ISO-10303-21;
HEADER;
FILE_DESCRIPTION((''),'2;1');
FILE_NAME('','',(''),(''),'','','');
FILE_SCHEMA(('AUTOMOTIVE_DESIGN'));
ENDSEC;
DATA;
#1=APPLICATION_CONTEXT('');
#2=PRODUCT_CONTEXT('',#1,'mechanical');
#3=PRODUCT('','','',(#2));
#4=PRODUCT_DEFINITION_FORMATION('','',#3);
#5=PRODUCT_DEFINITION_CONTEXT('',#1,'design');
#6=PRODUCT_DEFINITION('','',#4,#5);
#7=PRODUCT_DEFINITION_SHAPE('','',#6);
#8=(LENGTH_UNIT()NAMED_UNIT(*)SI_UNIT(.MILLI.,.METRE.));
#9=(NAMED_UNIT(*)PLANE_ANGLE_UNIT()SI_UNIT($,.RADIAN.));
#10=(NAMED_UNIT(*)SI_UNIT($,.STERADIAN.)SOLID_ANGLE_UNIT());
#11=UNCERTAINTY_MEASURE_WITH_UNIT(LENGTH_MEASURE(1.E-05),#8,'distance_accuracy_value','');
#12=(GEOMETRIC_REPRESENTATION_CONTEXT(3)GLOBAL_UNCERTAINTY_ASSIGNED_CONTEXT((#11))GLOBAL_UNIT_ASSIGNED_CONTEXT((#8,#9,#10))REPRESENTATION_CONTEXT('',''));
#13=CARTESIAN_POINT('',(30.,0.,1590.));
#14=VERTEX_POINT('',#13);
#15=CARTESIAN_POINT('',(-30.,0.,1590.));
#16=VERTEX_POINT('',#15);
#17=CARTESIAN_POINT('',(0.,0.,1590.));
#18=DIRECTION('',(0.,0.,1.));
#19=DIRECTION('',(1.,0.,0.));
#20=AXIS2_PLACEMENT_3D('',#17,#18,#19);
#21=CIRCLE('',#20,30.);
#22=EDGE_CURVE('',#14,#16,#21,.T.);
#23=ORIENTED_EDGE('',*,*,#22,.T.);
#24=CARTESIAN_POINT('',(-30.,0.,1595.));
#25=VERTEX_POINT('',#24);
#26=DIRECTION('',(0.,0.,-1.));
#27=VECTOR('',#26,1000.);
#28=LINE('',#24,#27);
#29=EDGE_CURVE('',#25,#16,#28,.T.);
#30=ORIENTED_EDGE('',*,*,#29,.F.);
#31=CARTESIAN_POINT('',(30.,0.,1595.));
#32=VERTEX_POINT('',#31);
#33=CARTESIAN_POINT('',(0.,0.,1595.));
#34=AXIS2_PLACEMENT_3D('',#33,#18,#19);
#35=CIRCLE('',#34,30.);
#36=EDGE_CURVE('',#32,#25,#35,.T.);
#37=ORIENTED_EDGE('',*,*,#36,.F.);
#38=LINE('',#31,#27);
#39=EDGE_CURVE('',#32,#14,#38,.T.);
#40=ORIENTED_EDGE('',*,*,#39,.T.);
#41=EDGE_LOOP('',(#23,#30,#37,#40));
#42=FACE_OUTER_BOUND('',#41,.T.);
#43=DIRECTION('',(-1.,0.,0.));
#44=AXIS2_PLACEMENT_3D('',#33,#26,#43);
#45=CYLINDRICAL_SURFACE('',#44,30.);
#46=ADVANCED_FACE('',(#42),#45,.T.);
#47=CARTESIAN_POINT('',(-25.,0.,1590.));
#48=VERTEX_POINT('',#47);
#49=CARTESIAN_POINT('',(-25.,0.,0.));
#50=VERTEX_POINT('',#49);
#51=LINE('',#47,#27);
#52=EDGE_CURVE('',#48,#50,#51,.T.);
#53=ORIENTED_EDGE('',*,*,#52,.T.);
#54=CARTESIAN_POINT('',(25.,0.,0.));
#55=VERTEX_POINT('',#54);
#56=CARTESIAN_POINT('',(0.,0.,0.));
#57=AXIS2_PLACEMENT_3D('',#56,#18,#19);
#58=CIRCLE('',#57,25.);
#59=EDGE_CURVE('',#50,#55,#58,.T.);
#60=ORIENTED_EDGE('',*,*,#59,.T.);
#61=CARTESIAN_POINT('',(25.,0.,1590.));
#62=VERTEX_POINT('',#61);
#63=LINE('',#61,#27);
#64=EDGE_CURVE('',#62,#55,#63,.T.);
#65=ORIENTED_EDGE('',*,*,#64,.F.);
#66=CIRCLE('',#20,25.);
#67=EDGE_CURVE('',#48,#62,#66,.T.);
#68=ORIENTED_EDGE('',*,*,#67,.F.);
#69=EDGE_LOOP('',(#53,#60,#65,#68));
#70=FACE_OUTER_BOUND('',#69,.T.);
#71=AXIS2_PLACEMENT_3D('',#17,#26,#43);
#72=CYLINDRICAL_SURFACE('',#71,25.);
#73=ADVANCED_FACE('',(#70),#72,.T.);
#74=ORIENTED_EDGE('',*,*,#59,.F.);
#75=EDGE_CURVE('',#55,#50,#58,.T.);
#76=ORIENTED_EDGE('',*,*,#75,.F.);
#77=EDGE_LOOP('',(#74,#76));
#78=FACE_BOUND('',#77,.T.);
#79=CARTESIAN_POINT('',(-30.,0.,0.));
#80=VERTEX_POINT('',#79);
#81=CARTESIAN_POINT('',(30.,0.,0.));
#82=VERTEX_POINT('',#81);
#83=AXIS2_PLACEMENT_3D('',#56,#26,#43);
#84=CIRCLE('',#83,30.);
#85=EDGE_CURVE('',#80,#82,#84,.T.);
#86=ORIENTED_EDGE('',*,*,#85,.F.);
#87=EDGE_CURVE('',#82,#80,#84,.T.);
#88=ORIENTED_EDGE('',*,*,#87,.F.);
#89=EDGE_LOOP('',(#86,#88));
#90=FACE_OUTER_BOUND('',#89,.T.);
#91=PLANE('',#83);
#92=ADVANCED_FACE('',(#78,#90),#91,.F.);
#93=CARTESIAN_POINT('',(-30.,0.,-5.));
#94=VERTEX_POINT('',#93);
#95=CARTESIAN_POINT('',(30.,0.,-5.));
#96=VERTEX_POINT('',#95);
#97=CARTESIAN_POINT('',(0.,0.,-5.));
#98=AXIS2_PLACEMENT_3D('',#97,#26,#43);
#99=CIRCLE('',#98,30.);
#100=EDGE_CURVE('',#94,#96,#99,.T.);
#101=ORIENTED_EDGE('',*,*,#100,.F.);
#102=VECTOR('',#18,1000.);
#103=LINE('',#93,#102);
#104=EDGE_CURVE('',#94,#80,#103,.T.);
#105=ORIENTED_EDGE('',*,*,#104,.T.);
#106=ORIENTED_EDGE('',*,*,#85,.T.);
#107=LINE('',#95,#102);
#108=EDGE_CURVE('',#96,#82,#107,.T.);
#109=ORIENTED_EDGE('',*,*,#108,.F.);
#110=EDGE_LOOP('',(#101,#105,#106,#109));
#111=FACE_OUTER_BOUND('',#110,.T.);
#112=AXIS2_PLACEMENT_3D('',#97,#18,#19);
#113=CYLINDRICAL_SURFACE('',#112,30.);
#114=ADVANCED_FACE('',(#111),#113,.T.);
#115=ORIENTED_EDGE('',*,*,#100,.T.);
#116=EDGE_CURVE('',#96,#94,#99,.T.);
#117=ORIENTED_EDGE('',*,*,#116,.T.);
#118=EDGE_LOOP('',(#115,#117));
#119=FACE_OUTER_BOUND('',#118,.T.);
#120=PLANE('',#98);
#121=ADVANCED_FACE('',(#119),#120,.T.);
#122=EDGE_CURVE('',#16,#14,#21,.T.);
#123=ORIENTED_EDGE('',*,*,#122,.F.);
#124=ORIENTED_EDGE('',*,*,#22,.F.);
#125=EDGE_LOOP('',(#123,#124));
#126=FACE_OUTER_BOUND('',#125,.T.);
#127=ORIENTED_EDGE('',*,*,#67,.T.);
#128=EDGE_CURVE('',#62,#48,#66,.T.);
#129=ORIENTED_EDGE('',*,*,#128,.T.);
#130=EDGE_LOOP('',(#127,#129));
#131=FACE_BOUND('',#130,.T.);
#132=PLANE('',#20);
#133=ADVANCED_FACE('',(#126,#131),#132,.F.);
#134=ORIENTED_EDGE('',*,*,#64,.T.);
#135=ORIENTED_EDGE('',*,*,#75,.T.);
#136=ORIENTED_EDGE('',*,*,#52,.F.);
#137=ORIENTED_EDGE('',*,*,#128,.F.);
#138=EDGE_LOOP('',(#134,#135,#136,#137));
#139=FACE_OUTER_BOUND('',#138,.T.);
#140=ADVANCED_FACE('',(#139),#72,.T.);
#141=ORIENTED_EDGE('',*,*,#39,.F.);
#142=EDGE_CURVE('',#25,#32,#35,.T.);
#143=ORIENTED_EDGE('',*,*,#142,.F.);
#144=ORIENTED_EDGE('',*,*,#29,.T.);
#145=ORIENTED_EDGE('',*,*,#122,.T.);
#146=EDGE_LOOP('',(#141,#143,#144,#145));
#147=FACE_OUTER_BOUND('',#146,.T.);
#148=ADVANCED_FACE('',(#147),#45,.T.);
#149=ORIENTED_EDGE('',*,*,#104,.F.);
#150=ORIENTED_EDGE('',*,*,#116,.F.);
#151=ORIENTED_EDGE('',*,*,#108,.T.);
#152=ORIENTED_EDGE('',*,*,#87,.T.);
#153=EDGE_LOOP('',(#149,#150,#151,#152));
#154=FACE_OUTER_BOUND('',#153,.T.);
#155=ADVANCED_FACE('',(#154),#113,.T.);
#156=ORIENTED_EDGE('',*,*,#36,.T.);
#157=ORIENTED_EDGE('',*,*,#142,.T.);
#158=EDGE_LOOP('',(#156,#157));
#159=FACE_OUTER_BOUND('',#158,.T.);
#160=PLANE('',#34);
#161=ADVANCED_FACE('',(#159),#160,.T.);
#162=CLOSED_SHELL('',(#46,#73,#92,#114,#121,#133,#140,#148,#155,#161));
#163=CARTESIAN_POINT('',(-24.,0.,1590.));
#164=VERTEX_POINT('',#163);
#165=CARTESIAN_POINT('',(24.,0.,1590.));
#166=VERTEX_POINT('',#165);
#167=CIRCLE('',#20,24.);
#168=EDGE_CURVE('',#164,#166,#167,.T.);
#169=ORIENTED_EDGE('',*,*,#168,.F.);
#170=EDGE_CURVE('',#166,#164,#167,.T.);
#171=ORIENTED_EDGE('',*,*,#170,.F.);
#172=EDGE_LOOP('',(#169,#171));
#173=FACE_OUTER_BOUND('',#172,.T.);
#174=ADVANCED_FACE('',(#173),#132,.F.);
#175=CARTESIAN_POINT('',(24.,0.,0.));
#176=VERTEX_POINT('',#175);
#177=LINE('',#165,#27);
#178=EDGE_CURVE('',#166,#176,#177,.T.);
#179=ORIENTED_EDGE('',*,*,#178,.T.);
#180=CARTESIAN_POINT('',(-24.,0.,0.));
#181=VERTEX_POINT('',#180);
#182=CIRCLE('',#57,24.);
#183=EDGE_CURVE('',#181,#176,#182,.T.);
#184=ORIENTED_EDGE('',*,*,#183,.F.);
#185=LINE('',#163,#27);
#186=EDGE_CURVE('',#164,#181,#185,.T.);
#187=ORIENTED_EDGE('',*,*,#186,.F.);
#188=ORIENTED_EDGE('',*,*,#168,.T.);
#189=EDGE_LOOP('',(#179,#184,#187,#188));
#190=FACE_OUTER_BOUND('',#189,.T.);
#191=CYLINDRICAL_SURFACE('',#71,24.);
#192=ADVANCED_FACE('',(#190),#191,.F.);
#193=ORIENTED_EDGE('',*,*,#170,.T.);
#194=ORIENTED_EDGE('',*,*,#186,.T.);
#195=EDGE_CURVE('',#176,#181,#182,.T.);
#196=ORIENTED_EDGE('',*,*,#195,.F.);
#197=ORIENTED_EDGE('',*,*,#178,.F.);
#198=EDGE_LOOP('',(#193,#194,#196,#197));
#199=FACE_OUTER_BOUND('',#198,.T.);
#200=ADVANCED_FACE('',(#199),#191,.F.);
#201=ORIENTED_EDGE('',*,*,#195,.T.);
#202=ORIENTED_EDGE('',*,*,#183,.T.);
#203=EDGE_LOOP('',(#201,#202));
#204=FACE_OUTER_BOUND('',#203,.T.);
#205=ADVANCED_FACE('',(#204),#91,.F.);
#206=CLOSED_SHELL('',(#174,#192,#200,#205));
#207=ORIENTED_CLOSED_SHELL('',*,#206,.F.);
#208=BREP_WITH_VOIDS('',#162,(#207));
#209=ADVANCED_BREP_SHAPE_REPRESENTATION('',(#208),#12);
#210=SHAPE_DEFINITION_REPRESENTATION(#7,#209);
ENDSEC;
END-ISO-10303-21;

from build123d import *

# Parameters (mm, degrees)
SKETCH1_R           = 25
SKETCH1_R_2         = 24
BOSS_EXTRUDE1_DEPTH = 1590
SKETCH4_R           = 30
BOSS_EXTRUDE2_DEPTH = 5
BOSS_EXTRUDE3_START = 5
SKETCH5_R           = 30
BOSS_EXTRUDE3_DEPTH = 5


with BuildPart() as part:
    # Sketch1 → Boss-Extrude1 (new body)
    with BuildSketch(Plane.XY):
        Circle(SKETCH1_R)
        Circle(SKETCH1_R_2, mode=Mode.SUBTRACT)
    extrude(amount=BOSS_EXTRUDE1_DEPTH)

    # Sketch4 → Boss-Extrude2 (add)
    with BuildSketch(Plane(origin=(0, 0, 0), x_dir=(-1, 0, 0), z_dir=(0, 0, -1))):
        Circle(SKETCH4_R)
    extrude(amount=BOSS_EXTRUDE2_DEPTH)

    # Sketch5 → Boss-Extrude3 (add)
    with BuildSketch(Plane.XY.offset(1590).offset(BOSS_EXTRUDE3_START)):
        with Locations(Location((0, 0, 0), (0, 0, 180))):
            Circle(SKETCH5_R)
    extrude(amount=-BOSS_EXTRUDE3_DEPTH)


solid = part.part
